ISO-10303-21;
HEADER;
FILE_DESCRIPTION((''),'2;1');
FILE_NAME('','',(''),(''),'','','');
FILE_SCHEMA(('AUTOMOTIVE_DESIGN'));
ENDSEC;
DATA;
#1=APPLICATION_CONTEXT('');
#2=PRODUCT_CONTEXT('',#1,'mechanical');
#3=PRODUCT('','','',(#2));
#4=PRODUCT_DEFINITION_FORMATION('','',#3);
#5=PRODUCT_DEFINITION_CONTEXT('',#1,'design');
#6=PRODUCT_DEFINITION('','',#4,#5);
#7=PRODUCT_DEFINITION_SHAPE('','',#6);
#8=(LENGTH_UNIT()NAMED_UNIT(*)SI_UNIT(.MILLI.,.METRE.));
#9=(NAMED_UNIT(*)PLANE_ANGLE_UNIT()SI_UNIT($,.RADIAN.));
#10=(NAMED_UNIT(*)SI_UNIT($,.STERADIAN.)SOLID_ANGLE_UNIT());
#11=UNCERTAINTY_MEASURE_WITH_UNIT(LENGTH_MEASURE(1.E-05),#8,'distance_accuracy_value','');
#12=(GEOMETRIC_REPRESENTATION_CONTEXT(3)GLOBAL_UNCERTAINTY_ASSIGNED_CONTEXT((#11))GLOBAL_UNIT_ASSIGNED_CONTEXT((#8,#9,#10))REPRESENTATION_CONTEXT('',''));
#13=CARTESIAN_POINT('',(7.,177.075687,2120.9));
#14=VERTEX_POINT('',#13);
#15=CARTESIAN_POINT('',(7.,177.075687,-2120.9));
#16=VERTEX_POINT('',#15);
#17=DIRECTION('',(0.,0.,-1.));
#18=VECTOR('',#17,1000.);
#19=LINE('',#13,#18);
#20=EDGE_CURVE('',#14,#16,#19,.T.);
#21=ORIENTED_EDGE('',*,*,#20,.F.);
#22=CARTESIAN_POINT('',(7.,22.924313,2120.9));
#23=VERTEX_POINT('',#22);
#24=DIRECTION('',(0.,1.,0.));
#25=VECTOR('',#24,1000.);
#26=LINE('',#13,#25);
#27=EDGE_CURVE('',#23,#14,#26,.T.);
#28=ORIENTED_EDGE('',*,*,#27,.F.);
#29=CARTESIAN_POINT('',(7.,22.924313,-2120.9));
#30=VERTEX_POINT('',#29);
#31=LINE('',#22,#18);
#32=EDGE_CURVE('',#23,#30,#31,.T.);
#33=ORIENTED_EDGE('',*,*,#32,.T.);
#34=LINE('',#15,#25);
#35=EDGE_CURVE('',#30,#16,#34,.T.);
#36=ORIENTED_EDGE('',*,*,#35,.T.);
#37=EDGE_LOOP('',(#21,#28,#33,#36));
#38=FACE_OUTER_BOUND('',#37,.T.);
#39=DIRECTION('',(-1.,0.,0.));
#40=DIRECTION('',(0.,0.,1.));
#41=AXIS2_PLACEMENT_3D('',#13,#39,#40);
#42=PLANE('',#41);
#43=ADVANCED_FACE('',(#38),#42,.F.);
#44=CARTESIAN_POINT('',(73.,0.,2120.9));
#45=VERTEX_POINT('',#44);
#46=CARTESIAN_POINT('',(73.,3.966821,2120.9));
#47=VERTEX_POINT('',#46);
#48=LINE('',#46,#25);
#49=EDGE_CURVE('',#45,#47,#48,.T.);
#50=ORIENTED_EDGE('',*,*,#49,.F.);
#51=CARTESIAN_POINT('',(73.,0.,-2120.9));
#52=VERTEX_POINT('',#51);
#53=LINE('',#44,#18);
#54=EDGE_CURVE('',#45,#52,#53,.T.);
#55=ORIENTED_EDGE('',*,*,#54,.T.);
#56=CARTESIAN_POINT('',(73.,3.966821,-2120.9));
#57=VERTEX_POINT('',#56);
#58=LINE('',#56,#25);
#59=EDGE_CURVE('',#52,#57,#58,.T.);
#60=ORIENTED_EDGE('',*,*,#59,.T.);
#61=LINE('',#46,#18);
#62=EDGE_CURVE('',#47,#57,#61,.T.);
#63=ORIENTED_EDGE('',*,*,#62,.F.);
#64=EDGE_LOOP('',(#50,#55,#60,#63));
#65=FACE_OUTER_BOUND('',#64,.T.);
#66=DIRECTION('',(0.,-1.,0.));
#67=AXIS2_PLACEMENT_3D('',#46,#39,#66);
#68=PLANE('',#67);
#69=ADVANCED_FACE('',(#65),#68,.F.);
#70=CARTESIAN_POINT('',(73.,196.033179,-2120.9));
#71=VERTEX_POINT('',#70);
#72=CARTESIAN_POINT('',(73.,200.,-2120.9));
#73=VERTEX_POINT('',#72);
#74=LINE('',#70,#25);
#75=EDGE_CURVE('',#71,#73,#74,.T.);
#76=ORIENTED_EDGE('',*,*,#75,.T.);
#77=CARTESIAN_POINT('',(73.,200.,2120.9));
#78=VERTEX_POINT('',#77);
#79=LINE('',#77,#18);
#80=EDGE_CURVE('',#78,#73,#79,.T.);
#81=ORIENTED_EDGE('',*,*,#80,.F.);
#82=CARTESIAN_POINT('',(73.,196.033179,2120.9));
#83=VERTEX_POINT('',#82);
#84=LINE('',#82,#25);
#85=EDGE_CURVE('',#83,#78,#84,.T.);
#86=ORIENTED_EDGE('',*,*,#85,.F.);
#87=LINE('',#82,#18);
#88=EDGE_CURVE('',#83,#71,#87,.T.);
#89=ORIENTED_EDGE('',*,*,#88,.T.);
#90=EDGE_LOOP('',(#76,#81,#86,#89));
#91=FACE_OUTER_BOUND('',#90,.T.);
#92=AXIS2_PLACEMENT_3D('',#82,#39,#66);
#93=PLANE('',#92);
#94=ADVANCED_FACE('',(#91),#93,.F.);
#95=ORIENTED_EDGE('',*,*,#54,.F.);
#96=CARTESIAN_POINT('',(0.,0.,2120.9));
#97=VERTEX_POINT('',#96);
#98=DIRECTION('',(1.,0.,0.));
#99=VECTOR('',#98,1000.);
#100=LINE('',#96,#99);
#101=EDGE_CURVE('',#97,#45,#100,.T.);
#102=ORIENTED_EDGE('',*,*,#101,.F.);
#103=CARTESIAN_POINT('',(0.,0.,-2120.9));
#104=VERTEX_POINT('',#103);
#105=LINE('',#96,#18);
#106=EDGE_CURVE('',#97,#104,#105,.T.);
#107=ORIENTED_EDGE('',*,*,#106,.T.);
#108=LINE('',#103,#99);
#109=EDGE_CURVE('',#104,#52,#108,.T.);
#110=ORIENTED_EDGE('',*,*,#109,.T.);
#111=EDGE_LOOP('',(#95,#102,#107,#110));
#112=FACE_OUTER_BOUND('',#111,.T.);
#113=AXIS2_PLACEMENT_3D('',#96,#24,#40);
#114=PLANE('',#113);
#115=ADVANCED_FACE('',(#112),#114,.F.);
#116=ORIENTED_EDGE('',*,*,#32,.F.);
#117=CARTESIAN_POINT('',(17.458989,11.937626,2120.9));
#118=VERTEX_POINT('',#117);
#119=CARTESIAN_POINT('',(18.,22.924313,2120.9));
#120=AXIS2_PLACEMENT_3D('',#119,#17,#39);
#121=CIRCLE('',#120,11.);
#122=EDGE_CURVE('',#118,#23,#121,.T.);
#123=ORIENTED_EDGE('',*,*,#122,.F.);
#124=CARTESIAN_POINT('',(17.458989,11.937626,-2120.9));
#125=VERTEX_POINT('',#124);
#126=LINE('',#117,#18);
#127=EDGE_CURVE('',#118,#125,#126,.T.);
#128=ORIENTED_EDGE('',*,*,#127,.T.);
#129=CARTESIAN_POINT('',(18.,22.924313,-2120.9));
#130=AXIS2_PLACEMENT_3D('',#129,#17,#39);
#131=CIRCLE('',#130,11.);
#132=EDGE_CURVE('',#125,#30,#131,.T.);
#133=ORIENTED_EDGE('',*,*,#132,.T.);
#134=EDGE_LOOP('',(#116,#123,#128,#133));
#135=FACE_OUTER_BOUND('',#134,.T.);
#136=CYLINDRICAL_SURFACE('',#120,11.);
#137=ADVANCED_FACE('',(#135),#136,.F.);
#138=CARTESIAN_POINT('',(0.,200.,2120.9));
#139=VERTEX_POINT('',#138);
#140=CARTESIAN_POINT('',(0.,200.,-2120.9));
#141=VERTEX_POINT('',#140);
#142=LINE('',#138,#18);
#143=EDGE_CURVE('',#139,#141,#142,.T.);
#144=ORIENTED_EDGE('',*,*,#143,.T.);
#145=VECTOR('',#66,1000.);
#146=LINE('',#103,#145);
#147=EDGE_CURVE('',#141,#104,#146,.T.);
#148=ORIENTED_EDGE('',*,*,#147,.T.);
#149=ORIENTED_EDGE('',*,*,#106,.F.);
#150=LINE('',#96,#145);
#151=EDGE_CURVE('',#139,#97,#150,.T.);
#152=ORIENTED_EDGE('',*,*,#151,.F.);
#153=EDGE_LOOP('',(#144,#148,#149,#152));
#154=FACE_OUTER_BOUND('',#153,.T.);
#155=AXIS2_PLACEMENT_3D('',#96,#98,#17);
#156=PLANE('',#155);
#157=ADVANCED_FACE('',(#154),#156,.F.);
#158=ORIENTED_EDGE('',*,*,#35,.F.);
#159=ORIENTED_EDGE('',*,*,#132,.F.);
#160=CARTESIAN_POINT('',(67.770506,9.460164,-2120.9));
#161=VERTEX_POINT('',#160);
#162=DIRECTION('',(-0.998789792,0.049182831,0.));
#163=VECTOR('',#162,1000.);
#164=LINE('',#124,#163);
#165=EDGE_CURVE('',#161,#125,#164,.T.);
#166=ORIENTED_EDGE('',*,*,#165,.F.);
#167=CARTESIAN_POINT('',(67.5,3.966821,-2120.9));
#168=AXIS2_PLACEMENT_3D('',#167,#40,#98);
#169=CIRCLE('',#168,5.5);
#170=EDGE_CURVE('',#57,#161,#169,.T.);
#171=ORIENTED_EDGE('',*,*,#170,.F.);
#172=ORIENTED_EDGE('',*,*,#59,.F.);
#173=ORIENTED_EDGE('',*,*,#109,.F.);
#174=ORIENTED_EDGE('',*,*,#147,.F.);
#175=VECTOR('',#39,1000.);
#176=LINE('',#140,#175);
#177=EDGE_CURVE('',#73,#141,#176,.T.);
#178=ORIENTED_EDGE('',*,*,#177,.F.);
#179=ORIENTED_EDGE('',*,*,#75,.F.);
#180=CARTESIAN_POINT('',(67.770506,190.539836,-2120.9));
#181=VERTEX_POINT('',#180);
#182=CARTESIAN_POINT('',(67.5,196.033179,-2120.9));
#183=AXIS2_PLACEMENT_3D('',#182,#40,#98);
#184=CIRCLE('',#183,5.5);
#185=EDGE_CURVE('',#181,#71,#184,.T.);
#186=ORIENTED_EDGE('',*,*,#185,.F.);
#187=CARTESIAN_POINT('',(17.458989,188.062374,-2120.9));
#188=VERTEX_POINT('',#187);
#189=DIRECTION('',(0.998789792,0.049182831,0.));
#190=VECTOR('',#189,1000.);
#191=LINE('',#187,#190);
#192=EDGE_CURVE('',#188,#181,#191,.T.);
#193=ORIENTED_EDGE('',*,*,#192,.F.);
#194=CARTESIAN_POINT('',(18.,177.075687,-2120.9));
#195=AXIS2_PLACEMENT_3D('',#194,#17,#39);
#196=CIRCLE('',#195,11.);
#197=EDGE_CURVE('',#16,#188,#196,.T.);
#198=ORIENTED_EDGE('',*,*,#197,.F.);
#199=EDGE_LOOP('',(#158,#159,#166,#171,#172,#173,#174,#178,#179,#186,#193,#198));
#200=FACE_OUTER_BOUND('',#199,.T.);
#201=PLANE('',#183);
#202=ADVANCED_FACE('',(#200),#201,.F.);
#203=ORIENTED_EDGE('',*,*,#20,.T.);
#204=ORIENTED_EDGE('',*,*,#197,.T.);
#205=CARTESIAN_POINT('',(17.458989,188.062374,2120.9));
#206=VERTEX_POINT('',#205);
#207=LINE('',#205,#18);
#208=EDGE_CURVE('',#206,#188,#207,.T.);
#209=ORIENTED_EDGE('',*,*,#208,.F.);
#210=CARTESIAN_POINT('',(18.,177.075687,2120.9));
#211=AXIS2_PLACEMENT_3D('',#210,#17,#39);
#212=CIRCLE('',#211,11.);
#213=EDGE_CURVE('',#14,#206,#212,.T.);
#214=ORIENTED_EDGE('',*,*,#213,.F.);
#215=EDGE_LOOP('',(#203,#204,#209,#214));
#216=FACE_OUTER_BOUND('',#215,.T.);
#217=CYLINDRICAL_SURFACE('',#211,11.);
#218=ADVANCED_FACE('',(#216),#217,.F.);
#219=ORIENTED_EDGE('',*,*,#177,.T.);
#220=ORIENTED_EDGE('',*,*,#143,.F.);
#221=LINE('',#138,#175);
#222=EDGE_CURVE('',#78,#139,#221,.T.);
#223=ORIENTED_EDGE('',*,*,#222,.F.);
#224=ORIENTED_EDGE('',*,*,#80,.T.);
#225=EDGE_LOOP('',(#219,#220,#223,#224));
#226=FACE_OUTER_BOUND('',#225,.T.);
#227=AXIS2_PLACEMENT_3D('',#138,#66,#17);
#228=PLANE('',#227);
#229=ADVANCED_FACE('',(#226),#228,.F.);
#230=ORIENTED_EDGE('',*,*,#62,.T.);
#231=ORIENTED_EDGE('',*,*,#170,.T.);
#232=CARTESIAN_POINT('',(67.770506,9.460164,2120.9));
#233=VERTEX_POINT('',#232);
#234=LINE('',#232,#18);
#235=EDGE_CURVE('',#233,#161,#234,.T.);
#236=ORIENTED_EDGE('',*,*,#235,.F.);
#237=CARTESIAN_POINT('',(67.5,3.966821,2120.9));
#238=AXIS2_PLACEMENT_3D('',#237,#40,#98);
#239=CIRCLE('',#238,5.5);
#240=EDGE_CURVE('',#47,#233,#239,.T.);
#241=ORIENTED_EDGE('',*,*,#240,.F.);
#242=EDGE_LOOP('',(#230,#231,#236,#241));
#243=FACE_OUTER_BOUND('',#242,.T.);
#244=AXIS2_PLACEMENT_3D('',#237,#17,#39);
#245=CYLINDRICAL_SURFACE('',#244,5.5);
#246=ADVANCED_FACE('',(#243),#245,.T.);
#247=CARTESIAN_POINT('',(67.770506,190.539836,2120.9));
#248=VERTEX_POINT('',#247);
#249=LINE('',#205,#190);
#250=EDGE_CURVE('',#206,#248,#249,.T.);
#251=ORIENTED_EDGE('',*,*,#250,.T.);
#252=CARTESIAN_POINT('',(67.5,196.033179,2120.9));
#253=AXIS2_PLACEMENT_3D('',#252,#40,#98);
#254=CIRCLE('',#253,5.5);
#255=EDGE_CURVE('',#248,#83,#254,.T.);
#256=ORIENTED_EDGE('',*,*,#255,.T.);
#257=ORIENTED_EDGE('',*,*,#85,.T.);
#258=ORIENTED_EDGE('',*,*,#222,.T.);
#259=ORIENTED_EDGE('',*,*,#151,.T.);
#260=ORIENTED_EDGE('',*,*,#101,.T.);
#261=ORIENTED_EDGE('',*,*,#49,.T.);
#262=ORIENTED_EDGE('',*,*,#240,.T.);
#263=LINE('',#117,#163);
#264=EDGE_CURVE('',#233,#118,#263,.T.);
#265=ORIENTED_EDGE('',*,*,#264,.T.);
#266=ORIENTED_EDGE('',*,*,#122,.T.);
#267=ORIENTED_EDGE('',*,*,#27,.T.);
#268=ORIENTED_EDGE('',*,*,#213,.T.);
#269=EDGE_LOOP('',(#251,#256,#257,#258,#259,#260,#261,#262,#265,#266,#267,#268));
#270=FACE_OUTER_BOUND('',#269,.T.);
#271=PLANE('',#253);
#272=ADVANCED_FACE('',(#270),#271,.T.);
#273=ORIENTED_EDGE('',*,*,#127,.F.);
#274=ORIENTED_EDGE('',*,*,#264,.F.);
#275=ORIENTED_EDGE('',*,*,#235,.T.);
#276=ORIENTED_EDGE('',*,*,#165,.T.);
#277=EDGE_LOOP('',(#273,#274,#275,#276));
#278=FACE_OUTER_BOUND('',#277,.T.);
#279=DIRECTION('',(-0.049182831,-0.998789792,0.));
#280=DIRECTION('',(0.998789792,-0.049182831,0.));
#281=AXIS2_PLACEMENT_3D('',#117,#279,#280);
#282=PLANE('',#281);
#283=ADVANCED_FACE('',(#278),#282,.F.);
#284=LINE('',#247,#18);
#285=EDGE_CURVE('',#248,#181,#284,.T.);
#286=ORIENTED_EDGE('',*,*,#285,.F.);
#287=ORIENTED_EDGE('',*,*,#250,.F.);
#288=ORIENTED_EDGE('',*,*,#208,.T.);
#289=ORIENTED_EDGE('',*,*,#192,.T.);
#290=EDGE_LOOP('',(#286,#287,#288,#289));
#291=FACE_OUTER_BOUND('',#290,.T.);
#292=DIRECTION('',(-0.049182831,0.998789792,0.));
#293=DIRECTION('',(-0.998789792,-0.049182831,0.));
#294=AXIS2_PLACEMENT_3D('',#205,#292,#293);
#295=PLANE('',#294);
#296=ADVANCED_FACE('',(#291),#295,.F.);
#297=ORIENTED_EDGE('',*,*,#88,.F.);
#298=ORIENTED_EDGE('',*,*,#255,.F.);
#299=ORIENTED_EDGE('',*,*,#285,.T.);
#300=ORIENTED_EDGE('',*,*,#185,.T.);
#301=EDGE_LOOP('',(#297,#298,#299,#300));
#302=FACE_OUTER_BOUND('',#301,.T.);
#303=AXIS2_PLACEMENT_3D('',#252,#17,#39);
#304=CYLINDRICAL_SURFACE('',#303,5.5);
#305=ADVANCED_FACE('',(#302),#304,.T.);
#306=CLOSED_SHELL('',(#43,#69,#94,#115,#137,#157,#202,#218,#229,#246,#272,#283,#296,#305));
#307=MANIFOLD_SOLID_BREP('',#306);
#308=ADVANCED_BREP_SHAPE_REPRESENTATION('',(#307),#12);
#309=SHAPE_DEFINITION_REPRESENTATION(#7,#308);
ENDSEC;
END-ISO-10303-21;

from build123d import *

# Parameters (mm, degrees)
BOSS_EXTRUDE1_DEPTH = 2120.9


with BuildPart() as part:
    # Sketch1 → Boss-Extrude1 (new, symmetric)
    with BuildSketch(Plane(origin=(28.211262136, 0, 0), x_dir=(-1, 0, 0), z_dir=(0, 0, 1))):
        with BuildLine():
            Line((28.211262136, 0), (28.211262136, -200))
            Line((28.211262136, -200), (-44.788737864, -200))
            Line((-44.788737864, -200), (-44.788737864, -196.033179359))
            ThreePointArc((-44.788737864, -196.033179359), (-43.272315441, -192.240936001), (-39.559243433, -190.539835501))
            Line((-39.559243433, -190.539835501), (10.752273273, -188.062374452))
            ThreePointArc((10.752273273, -188.062374452), (18.17841729, -184.660173452), (21.211262136, -177.075686736))
            Line((21.211262136, -177.075686736), (21.211262136, -22.924313264))
            ThreePointArc((21.211262136, -22.924313264), (18.17841729, -15.339826548), (10.752273273, -11.937625548))
            Line((10.752273273, -11.937625548), (-39.559243433, -9.460164499))
            ThreePointArc((-39.559243433, -9.460164499), (-43.272315441, -7.759063999), (-44.788737864, -3.966820641))
            Line((-44.788737864, -3.966820641), (-44.788737864, 0))
            Line((-44.788737864, 0), (28.211262136, 0))
        make_face()
    extrude(amount=BOSS_EXTRUDE1_DEPTH, both=True)


solid = part.part
